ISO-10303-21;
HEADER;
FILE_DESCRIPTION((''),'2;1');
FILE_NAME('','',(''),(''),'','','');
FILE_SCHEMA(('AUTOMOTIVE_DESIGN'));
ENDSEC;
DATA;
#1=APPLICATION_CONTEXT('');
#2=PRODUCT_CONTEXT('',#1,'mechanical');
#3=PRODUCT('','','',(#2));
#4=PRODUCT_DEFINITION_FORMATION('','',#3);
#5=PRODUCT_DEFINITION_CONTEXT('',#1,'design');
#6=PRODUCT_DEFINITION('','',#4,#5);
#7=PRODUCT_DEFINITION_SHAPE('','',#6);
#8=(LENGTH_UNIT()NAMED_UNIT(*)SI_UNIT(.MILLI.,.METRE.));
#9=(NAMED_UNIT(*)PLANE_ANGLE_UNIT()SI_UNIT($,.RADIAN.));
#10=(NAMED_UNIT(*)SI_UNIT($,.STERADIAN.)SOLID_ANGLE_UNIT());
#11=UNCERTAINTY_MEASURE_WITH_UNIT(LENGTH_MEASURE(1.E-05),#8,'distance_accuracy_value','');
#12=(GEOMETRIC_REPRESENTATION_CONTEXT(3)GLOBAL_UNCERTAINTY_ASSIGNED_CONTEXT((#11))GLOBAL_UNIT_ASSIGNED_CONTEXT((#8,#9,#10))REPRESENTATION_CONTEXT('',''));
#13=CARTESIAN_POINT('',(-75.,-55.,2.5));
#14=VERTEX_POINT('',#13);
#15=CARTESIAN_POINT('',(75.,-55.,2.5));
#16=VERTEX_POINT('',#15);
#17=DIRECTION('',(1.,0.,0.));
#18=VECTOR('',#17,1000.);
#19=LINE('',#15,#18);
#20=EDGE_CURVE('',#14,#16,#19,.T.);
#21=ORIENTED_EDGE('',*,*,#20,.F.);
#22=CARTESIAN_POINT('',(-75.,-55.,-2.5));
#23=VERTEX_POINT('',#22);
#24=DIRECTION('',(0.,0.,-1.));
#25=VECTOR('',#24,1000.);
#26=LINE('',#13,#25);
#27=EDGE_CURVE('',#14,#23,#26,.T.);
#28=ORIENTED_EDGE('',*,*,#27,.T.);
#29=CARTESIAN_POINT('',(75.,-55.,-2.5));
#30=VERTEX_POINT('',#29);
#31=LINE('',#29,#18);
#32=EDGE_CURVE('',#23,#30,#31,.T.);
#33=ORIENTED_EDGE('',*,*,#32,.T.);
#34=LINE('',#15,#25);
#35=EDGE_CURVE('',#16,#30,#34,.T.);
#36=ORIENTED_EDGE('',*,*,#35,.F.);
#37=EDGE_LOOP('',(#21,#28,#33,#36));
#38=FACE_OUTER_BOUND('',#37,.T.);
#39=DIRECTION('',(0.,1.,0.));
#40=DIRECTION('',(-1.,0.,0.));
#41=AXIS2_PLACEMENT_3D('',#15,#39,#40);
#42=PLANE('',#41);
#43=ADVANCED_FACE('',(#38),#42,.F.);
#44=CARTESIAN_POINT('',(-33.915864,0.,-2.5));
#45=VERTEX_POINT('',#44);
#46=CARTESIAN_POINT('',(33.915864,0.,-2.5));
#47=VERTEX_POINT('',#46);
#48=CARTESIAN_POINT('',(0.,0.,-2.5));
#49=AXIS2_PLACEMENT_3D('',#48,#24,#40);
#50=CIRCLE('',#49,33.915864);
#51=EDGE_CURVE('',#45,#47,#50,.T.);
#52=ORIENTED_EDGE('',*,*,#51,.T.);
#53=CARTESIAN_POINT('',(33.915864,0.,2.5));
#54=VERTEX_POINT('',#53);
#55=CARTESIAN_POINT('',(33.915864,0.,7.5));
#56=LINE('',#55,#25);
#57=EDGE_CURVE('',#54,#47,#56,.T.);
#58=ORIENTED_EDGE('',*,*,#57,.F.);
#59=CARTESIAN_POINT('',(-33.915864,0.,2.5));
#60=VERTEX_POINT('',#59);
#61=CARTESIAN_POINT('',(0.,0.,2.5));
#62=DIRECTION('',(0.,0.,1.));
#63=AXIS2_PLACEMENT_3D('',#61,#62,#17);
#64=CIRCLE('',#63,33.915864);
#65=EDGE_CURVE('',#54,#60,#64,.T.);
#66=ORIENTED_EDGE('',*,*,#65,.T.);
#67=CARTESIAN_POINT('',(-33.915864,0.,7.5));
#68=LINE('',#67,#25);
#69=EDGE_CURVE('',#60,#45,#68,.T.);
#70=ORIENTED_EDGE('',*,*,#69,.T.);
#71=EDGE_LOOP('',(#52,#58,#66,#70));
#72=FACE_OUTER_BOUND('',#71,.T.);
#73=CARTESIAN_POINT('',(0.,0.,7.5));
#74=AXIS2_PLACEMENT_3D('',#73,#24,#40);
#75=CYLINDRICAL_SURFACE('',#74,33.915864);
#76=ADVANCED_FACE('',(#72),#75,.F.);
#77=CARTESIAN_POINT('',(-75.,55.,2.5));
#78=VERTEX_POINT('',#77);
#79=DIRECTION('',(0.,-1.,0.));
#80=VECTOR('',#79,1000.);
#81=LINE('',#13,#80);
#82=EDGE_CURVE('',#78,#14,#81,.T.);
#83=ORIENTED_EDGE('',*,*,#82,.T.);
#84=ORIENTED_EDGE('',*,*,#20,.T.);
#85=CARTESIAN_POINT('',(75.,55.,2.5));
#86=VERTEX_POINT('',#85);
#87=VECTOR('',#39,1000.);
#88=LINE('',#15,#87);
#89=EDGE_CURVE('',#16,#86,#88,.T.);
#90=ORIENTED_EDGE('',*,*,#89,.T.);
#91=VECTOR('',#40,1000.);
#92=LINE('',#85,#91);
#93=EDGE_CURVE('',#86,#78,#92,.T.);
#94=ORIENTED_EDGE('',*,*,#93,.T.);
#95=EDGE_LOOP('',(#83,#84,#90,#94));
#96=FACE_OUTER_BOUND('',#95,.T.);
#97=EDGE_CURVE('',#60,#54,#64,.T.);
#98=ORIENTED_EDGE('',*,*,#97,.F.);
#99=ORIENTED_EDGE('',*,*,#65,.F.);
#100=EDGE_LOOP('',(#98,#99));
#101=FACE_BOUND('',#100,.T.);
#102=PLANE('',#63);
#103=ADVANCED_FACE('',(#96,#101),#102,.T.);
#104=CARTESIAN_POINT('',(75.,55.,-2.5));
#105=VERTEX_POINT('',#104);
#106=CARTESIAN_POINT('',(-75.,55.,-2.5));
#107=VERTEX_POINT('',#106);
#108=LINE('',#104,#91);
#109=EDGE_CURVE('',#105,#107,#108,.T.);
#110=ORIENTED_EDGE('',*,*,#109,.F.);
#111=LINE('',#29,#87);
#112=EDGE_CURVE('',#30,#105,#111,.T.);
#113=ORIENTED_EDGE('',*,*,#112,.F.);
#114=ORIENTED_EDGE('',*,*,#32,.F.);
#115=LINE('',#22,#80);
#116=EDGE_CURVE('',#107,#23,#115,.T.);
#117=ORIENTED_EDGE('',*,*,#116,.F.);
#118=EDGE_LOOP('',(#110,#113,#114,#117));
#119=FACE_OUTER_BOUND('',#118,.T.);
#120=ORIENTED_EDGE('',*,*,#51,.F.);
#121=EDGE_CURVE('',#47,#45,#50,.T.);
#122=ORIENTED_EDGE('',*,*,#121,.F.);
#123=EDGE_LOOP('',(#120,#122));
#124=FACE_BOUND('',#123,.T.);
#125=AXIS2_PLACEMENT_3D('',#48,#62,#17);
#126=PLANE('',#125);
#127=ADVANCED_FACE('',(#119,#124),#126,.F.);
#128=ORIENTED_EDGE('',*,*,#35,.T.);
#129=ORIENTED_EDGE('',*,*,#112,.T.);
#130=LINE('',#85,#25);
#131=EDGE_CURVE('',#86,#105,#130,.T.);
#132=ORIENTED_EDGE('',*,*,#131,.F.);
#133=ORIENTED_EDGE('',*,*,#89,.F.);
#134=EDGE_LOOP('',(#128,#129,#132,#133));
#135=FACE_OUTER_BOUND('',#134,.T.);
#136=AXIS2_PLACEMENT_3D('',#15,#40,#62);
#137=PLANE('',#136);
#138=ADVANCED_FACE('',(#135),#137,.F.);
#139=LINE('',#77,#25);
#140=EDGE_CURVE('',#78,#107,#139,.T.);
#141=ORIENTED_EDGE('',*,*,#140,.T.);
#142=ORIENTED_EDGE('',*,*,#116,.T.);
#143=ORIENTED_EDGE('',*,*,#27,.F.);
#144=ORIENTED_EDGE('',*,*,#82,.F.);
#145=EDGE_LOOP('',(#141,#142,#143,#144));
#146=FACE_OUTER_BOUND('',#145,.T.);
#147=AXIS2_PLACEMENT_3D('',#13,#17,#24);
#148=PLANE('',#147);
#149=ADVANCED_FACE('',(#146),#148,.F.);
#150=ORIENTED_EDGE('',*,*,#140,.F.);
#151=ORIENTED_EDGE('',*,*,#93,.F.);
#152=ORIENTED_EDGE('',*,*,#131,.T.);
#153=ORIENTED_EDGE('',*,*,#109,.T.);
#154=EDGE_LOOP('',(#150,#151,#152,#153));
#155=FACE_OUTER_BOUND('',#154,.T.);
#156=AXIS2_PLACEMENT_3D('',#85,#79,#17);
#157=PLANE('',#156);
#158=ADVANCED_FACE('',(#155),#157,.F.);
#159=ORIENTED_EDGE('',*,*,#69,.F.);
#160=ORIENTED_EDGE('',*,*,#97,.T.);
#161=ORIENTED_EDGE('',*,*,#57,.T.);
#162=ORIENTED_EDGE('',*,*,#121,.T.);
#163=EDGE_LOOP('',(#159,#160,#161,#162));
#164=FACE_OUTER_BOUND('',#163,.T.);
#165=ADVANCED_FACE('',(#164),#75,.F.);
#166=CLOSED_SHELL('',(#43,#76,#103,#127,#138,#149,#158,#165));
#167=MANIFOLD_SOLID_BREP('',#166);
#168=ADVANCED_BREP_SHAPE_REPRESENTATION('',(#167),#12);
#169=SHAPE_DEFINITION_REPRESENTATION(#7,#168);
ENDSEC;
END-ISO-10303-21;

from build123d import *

# Parameters (mm, degrees)
SKETCH_1_W          = 150
SKETCH_1_H          = 110
EXTRUDE_1_DEPTH     = 2.5
SKETCH_2_R          = 33.915864145
CUT_EXTRUDE_1_DEPTH = 10


with BuildPart() as part:
    # 草图1 → 凸台-拉伸1 (new, symmetric)
    with BuildSketch(Plane.XY):
        Rectangle(SKETCH_1_W, SKETCH_1_H)
    extrude(amount=EXTRUDE_1_DEPTH, both=True)

    # 草图2 → 切除-拉伸1 (cut)
    with BuildSketch(Plane(origin=(0, 0, -2.5), x_dir=(-1, 0, 0), z_dir=(0, 0, -1))):
        Circle(SKETCH_2_R)
    extrude(amount=-CUT_EXTRUDE_1_DEPTH, mode=Mode.SUBTRACT)


solid = part.part
